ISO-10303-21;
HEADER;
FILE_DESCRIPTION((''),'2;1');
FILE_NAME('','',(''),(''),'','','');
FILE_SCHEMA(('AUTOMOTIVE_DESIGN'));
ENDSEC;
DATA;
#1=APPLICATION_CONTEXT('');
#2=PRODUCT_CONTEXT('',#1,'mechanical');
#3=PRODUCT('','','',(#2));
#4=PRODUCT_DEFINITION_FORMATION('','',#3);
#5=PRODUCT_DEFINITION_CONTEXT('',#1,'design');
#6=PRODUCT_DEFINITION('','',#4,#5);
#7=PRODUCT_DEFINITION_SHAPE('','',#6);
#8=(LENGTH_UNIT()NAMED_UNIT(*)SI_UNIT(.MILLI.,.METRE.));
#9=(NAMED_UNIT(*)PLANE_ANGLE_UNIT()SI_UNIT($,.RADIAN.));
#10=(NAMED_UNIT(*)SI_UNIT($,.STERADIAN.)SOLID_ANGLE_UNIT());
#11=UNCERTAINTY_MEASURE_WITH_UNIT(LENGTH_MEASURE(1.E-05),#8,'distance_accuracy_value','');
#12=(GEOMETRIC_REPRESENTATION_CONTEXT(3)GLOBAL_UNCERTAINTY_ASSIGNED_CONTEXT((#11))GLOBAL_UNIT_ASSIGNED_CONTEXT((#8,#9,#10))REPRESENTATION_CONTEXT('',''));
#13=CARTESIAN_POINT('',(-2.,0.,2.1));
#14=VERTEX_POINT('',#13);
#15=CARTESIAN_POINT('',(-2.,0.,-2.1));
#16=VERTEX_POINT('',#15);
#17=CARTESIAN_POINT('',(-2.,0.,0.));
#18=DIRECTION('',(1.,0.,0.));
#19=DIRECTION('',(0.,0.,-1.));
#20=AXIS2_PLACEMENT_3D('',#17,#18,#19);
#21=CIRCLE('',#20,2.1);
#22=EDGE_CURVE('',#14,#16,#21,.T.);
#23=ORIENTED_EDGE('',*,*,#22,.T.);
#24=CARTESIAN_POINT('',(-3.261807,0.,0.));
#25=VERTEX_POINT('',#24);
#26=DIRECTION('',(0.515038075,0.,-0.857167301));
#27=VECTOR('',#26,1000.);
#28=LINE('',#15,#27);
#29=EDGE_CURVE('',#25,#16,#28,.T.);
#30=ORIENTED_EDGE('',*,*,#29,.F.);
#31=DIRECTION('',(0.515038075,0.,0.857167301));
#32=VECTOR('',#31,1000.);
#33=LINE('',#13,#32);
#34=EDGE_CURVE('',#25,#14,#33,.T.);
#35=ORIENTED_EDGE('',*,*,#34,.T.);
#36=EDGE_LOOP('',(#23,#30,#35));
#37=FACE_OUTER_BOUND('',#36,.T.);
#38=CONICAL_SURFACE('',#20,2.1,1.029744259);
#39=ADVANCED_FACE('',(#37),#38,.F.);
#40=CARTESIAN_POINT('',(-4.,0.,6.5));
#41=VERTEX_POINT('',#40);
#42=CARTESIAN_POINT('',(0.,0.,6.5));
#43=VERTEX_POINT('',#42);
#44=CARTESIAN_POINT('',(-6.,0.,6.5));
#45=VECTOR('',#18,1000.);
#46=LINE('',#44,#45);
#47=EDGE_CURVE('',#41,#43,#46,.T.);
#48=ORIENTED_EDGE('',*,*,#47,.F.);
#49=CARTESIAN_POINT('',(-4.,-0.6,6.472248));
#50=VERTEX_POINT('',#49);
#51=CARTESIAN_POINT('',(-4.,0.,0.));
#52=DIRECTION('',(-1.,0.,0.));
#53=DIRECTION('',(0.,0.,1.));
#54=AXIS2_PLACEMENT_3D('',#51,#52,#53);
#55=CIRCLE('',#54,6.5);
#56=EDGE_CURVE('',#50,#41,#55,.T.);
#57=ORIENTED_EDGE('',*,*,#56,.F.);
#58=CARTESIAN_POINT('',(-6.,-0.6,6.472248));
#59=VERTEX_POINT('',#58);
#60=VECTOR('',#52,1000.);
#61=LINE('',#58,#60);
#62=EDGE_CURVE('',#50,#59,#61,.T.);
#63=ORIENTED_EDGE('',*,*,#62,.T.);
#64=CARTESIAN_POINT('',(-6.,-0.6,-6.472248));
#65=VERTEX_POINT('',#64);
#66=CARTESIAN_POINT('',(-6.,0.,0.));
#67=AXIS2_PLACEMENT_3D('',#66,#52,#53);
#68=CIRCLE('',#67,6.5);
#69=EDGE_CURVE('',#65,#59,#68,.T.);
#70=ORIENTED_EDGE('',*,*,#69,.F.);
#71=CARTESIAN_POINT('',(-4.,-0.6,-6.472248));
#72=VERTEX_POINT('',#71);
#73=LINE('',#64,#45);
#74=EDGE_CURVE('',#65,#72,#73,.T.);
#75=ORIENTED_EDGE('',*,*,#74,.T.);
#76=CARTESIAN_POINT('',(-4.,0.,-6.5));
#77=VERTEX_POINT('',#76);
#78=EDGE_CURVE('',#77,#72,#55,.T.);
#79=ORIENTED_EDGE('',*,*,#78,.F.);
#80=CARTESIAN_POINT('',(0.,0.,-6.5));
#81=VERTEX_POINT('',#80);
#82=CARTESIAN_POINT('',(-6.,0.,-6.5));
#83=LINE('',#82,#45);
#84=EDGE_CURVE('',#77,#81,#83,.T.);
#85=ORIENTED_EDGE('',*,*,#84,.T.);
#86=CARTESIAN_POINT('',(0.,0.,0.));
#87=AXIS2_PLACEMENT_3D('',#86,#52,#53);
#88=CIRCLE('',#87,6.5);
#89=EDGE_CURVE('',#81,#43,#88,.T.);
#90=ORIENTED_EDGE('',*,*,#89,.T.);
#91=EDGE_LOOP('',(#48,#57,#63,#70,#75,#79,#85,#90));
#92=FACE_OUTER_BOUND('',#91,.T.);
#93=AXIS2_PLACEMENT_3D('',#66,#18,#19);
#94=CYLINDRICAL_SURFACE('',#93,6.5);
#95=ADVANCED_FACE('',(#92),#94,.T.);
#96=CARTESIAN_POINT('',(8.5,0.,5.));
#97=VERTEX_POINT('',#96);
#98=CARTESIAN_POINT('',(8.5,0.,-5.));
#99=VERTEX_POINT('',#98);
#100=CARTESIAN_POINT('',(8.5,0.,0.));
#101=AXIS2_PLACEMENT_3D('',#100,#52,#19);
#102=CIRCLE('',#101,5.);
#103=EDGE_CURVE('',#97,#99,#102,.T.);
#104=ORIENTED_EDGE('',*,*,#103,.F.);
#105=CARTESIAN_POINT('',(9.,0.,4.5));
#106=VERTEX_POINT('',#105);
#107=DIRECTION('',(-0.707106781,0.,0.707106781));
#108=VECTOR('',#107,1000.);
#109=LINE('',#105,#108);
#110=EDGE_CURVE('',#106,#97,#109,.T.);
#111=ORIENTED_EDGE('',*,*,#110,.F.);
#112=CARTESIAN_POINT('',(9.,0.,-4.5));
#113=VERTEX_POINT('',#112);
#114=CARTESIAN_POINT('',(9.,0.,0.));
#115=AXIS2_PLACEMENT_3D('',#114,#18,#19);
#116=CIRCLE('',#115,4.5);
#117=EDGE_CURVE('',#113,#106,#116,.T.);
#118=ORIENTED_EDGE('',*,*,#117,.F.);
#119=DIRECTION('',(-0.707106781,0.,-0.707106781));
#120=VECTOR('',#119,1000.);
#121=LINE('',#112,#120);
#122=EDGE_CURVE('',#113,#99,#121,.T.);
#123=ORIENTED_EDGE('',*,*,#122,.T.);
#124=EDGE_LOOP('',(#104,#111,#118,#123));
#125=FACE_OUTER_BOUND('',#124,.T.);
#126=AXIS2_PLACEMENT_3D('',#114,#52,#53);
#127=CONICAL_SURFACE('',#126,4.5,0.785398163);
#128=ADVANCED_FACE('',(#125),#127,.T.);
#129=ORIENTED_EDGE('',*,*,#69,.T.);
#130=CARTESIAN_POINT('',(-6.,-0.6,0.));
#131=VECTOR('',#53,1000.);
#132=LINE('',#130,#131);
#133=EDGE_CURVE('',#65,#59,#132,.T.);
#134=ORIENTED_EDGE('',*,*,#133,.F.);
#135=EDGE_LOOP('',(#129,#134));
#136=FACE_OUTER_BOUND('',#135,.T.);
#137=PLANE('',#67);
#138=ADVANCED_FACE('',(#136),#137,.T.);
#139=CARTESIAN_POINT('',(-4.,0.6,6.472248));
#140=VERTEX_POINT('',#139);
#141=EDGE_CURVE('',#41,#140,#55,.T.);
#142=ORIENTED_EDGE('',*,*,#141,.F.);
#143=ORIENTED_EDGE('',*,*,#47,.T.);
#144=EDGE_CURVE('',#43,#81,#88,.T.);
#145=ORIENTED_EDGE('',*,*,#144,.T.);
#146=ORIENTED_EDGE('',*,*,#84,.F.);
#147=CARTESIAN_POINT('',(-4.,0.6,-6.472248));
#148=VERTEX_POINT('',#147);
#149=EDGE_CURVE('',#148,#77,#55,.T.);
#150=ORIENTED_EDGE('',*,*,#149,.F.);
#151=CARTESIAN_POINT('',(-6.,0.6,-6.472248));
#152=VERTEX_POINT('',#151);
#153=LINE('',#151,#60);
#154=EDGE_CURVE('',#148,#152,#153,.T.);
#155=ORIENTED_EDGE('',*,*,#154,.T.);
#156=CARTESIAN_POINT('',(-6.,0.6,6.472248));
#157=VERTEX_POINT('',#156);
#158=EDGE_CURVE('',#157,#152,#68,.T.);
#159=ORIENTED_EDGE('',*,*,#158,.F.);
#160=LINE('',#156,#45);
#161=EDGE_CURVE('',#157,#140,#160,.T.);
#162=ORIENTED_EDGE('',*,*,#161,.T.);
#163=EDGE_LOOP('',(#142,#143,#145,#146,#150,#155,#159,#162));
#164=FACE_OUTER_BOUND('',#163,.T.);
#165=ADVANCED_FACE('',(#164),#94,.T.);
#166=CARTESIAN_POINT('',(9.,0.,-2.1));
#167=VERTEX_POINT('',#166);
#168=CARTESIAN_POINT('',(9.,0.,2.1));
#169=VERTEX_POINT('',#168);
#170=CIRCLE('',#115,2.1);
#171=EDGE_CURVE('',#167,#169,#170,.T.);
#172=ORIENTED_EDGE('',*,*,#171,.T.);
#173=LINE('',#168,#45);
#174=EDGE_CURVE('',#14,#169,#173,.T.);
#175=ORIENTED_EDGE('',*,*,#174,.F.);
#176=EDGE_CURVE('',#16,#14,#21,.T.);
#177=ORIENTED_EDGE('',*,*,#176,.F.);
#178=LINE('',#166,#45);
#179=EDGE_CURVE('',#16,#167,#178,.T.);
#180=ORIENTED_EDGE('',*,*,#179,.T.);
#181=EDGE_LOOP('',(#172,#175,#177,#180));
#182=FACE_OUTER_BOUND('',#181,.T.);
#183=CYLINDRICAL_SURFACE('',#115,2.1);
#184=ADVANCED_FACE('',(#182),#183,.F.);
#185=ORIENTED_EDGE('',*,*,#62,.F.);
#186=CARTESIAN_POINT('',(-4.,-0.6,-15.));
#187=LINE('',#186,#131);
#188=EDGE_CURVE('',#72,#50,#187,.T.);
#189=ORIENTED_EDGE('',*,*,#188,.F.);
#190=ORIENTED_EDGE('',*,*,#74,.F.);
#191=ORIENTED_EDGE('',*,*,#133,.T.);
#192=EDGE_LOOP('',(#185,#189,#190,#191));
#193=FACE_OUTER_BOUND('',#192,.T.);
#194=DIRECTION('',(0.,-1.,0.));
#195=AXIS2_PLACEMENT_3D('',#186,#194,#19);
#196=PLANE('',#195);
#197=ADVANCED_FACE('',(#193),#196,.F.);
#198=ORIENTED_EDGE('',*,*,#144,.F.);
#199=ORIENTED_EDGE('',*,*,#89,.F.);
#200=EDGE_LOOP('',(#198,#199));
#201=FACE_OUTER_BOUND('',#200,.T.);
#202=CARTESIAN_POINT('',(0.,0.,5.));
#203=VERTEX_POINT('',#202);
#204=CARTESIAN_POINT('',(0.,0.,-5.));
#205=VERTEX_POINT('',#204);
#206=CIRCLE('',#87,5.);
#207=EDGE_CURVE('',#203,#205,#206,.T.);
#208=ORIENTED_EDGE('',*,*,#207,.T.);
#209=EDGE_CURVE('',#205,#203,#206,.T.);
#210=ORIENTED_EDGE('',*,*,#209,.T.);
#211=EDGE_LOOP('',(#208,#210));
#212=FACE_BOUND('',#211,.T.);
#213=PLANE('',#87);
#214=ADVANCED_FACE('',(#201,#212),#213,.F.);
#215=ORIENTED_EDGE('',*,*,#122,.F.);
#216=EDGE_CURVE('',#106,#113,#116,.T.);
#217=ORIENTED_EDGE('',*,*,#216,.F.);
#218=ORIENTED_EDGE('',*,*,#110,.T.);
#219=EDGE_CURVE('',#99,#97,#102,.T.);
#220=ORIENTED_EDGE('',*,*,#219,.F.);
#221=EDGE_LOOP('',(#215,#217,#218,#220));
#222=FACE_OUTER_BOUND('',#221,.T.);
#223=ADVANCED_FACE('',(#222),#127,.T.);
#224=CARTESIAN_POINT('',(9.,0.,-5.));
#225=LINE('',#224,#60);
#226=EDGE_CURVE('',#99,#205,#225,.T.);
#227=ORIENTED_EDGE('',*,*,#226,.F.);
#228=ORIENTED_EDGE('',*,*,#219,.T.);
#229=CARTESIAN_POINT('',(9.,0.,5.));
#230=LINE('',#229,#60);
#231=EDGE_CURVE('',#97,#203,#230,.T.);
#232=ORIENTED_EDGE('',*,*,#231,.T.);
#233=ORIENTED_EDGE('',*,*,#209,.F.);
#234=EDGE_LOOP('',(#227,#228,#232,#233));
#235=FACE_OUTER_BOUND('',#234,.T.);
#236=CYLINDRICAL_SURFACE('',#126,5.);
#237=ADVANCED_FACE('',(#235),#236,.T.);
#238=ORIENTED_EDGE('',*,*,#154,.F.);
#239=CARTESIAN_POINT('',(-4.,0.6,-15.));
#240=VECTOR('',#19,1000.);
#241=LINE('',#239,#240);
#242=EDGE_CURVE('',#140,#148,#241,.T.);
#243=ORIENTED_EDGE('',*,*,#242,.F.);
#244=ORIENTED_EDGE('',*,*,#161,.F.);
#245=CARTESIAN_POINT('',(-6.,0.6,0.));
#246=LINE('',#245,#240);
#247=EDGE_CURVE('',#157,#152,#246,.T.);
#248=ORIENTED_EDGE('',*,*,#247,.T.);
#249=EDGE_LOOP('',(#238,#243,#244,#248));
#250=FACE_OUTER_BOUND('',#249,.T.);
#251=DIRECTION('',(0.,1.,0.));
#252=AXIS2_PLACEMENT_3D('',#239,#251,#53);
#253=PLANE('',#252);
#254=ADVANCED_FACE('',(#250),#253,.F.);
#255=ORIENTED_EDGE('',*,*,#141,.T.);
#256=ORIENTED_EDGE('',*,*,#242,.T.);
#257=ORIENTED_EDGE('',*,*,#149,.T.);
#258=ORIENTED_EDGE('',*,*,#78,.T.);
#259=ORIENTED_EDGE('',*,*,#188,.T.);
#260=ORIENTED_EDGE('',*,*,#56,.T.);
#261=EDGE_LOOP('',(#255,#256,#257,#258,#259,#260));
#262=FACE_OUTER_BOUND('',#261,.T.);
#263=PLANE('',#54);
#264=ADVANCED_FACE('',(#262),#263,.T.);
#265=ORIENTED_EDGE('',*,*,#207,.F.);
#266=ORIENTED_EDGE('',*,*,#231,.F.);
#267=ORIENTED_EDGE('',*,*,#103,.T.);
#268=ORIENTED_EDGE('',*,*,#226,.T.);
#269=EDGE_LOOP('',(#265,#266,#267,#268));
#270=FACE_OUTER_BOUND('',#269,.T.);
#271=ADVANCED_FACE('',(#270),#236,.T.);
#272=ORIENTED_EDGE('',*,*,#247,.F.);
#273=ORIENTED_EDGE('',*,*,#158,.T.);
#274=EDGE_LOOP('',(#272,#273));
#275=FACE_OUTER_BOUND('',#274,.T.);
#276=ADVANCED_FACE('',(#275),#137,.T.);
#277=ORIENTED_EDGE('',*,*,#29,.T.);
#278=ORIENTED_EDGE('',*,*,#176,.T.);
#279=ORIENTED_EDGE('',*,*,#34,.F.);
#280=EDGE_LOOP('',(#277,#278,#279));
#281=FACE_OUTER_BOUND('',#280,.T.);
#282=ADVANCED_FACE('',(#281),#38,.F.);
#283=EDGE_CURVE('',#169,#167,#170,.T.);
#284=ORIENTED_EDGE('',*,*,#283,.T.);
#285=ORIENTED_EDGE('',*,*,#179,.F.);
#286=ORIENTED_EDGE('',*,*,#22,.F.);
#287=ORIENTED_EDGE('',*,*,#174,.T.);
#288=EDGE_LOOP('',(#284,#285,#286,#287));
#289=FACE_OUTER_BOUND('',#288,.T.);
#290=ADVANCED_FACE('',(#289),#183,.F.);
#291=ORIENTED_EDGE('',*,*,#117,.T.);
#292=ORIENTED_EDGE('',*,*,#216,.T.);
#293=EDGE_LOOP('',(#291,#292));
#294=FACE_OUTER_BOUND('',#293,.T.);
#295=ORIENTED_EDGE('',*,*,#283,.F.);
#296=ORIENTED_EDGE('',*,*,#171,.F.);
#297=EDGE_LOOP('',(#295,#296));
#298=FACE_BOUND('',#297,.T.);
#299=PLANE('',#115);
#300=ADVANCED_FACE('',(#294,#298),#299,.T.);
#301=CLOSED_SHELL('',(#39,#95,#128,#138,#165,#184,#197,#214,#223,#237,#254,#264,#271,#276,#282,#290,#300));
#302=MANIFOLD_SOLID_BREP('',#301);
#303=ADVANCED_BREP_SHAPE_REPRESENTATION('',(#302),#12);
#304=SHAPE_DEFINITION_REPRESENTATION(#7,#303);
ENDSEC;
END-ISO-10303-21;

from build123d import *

# Parameters (mm, degrees)
SKETCH_2_R             = 5
EXTRUDE_1_DEPTH        = 9
SKETCH_5_R             = 6.5
EXTRUDE_2_DEPTH        = 6
SKETCH_6_W             = 30
SKETCH_6_H             = 1.2
CUT_EXTRUDE_1_DEPTH    = 2
HOLE_WIZARD_M5_1_D     = 4.2
HOLE_WIZARD_M5_1_DEPTH = 11
HOLE_WIZARD_M5_1_TIP   = 1.2618073
CHAMFER_1_SIZE         = 0.5


with BuildPart() as part:
    # 草图2 → 凸台-拉伸1 (new body)
    with BuildSketch(Plane(origin=(0, 0, 0), x_dir=(0, 0, -1), z_dir=(1, 0, 0))):
        Circle(SKETCH_2_R)
    extrude(amount=EXTRUDE_1_DEPTH)

    # 草图5 → 凸台-拉伸2 (add)
    with BuildSketch(Plane.ZY):
        Circle(SKETCH_5_R)
    extrude(amount=EXTRUDE_2_DEPTH)

    # 草图6 → 切除-拉伸1 (cut)
    with BuildSketch(Plane.ZY.offset(6)):
        Rectangle(SKETCH_6_W, SKETCH_6_H)
    extrude(amount=-CUT_EXTRUDE_1_DEPTH, mode=Mode.SUBTRACT)

    # M5 螺纹孔1
    with Locations(Plane(origin=(9, 0, 0), x_dir=(0, 0, 1), z_dir=(1, 0, 0))):
        with Locations((0, 0)):
            Hole(HOLE_WIZARD_M5_1_D / 2, depth=HOLE_WIZARD_M5_1_DEPTH)
            with Locations((0, 0, -(HOLE_WIZARD_M5_1_DEPTH + HOLE_WIZARD_M5_1_TIP / 2))):  # 118° drill point
                Cone(0, HOLE_WIZARD_M5_1_D / 2, HOLE_WIZARD_M5_1_TIP, mode=Mode.SUBTRACT)

    # 倒角1
    chamfer_1_edges = [part.edges().sort_by_distance(p)[0] for p in [
        (9, 0, 5),
    ]]
    chamfer(chamfer_1_edges, length=CHAMFER_1_SIZE)


solid = part.part
